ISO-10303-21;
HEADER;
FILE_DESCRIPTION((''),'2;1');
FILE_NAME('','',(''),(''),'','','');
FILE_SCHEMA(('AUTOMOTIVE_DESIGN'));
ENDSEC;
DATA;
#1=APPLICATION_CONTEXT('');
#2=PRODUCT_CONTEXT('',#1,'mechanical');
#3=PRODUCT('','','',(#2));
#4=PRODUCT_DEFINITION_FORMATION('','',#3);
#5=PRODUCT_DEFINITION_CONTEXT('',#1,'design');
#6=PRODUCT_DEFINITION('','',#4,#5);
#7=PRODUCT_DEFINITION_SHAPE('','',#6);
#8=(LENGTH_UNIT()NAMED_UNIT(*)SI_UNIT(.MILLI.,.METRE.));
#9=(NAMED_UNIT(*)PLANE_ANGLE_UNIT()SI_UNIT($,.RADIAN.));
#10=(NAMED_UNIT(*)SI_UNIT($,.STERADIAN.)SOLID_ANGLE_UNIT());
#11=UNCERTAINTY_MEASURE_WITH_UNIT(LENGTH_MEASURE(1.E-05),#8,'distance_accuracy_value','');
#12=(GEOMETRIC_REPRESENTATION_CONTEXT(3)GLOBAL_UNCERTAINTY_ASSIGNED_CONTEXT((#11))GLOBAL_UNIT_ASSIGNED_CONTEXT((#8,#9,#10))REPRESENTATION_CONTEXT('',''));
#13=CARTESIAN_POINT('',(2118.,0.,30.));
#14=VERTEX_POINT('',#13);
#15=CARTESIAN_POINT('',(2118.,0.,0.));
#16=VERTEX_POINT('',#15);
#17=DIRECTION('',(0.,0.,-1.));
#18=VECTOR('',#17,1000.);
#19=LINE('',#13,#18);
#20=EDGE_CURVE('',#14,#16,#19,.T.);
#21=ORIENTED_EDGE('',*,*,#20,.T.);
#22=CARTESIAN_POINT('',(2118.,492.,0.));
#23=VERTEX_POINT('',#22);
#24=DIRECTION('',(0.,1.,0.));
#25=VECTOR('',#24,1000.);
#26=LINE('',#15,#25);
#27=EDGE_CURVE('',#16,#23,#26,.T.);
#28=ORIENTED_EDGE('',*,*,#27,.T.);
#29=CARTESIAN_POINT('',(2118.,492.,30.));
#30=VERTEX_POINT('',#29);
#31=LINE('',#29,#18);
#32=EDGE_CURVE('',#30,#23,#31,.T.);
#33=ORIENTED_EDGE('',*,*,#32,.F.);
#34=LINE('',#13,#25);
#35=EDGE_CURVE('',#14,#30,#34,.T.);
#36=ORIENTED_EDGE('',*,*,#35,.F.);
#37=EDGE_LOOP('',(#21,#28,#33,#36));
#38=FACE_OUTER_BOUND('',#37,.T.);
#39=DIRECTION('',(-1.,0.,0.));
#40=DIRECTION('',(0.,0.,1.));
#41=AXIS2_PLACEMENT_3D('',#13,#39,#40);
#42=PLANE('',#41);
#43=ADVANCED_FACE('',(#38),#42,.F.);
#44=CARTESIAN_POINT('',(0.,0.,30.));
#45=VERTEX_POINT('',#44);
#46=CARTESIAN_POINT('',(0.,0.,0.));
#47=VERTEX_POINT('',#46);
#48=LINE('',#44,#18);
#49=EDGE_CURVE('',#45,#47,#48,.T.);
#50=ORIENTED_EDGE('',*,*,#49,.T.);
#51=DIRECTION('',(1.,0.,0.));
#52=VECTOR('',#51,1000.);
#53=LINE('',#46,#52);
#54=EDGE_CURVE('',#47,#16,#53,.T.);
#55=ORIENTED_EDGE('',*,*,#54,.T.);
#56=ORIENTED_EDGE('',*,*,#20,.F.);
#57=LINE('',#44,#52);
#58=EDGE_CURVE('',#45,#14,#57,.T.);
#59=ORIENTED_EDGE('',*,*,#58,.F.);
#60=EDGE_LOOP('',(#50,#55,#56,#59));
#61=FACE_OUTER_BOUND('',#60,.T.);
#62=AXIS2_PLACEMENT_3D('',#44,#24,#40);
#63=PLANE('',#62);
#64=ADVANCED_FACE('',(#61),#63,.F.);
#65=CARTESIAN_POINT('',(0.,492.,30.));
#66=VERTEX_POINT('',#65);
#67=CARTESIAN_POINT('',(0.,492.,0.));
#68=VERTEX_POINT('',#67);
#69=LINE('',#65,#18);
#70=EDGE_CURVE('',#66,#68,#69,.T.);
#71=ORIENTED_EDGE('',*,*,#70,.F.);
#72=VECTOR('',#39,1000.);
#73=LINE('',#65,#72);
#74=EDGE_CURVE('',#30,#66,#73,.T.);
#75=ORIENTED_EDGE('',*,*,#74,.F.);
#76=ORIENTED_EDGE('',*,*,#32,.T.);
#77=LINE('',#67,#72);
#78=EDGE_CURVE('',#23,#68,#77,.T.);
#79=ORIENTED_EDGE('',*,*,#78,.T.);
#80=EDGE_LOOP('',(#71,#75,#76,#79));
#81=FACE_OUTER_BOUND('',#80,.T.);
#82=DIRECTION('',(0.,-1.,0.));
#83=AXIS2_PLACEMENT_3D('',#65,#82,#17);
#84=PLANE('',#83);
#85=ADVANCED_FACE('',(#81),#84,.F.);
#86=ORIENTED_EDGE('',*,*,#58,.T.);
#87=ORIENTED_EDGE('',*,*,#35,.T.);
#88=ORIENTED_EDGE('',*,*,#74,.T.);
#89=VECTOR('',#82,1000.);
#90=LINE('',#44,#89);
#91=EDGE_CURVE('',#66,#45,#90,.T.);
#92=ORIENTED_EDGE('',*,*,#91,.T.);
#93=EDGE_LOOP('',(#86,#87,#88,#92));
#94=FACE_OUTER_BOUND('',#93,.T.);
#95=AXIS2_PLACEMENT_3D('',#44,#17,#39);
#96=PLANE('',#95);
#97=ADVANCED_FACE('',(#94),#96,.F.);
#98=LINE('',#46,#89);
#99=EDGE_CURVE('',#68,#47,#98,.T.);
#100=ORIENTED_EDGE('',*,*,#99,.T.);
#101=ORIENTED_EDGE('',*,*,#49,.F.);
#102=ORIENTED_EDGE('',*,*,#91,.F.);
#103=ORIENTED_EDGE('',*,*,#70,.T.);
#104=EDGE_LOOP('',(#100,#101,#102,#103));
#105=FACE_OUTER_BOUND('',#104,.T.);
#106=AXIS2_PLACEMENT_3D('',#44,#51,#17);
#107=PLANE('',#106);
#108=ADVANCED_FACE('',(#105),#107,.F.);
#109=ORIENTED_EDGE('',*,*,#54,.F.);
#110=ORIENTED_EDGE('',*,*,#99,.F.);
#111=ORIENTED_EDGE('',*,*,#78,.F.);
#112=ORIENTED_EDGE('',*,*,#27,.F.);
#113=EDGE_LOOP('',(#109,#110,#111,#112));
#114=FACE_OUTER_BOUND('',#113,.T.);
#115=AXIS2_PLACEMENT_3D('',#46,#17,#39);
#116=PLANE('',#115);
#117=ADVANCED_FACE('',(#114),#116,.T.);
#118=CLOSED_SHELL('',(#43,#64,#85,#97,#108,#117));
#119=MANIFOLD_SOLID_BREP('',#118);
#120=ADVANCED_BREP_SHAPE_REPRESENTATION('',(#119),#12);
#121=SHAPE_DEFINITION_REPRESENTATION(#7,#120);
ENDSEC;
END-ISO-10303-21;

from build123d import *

# Parameters (mm, degrees)
SKETCH1_W           = 2118
SKETCH1_H           = 492
BOSS_EXTRUDE1_DEPTH = 30


with BuildPart() as part:
    # Sketch1 → Boss-Extrude1 (new body)
    with BuildSketch(Plane.XY):
        with Locations((1059, 246)):
            Rectangle(SKETCH1_W, SKETCH1_H)
    extrude(amount=BOSS_EXTRUDE1_DEPTH)


solid = part.part
